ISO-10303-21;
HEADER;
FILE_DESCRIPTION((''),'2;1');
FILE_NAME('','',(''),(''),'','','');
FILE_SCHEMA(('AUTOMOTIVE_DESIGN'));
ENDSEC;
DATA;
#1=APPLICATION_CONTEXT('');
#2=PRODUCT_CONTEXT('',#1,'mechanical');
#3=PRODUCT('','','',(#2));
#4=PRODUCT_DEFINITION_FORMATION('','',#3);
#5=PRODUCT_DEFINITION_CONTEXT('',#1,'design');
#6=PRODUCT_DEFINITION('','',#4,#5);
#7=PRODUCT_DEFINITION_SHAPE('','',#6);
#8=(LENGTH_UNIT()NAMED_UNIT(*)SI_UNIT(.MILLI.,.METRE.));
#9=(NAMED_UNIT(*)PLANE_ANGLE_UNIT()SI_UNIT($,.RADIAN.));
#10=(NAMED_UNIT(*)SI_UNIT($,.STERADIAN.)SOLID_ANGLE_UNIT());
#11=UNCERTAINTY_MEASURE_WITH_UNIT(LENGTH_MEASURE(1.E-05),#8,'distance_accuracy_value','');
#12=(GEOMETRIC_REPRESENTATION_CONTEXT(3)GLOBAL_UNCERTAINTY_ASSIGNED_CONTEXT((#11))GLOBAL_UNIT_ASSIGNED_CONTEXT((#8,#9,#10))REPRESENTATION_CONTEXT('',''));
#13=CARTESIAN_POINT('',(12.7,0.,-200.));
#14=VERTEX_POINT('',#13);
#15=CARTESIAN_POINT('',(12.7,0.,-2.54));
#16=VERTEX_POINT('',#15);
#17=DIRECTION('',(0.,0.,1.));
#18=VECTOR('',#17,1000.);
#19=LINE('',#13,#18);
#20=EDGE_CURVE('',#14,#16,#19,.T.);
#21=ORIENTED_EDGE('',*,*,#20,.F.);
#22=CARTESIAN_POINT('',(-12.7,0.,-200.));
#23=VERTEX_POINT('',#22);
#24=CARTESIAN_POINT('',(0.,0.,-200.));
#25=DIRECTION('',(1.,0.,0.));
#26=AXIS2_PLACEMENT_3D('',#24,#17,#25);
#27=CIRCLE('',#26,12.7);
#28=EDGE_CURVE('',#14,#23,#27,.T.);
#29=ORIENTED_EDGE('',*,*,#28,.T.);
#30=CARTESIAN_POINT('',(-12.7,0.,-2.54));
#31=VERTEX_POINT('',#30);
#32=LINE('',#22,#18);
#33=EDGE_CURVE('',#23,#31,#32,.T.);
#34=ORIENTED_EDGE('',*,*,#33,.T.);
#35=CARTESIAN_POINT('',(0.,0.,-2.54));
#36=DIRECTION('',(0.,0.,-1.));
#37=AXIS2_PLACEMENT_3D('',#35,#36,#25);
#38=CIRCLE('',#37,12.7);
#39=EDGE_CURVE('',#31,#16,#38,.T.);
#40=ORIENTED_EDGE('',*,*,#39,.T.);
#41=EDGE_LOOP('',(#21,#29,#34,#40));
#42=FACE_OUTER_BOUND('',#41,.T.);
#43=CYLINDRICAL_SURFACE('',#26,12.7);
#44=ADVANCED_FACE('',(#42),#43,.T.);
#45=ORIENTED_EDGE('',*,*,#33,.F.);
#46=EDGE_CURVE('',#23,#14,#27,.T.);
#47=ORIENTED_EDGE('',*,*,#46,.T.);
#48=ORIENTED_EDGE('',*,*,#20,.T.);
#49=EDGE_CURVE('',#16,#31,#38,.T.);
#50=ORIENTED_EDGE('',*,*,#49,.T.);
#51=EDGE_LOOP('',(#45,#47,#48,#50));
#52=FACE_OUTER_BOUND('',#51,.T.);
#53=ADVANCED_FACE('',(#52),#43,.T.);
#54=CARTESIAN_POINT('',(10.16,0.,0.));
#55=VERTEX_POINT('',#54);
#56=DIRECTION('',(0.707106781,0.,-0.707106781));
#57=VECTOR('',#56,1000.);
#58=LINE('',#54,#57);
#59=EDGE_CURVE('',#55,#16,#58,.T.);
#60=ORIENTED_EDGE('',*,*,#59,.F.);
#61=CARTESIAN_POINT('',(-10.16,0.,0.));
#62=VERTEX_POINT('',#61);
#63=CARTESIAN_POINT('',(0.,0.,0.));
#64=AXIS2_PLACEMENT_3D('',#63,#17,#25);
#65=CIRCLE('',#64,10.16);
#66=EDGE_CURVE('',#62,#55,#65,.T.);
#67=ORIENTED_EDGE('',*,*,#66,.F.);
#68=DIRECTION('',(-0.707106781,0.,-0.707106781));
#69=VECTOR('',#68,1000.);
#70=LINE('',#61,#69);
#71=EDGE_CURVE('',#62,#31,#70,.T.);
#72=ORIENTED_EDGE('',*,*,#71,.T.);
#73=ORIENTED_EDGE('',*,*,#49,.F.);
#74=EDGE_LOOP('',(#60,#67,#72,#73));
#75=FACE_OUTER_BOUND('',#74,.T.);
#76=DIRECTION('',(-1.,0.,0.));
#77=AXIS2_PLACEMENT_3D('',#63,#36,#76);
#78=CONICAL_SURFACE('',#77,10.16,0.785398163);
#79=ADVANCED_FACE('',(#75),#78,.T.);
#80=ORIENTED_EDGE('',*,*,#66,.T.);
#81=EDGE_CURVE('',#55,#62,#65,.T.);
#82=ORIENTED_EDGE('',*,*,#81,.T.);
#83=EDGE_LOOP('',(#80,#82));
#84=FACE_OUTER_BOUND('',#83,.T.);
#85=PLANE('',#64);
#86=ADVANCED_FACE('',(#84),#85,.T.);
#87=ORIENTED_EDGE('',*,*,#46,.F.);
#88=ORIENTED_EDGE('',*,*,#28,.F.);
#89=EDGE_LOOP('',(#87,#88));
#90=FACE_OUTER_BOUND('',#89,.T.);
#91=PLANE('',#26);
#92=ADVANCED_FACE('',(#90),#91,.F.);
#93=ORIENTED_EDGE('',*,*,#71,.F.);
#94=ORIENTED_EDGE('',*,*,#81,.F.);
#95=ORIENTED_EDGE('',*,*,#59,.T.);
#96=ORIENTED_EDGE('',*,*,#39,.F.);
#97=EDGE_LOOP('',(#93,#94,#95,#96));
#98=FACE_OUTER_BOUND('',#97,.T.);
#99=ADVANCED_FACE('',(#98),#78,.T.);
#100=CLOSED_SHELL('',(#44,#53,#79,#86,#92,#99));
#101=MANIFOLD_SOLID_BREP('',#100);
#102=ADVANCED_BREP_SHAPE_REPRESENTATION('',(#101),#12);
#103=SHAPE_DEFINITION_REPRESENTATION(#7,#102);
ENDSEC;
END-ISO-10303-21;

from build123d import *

# Parameters (mm, degrees)
SKETCH1_R           = 6.35
BOSS_EXTRUDE1_DEPTH = 100
CHAMFER1_SIZE       = 1.27
SCALE1_SCALE        = 2


with BuildPart() as part:
    # Sketch1 → Boss-Extrude1 (new body)
    with BuildSketch(Plane.XY):
        Circle(SKETCH1_R)
    extrude(amount=-BOSS_EXTRUDE1_DEPTH)

    # Chamfer1
    chamfer1_edges = [part.edges().sort_by_distance(p)[0] for p in [
        (-6.35, 0, 0),
    ]]
    chamfer(chamfer1_edges, length=CHAMFER1_SIZE)


with BuildPart() as part_1:
    # Scale1: scaled about (0, 0, 0)
    add(part.part.scale(SCALE1_SCALE))


solid = part_1.part
